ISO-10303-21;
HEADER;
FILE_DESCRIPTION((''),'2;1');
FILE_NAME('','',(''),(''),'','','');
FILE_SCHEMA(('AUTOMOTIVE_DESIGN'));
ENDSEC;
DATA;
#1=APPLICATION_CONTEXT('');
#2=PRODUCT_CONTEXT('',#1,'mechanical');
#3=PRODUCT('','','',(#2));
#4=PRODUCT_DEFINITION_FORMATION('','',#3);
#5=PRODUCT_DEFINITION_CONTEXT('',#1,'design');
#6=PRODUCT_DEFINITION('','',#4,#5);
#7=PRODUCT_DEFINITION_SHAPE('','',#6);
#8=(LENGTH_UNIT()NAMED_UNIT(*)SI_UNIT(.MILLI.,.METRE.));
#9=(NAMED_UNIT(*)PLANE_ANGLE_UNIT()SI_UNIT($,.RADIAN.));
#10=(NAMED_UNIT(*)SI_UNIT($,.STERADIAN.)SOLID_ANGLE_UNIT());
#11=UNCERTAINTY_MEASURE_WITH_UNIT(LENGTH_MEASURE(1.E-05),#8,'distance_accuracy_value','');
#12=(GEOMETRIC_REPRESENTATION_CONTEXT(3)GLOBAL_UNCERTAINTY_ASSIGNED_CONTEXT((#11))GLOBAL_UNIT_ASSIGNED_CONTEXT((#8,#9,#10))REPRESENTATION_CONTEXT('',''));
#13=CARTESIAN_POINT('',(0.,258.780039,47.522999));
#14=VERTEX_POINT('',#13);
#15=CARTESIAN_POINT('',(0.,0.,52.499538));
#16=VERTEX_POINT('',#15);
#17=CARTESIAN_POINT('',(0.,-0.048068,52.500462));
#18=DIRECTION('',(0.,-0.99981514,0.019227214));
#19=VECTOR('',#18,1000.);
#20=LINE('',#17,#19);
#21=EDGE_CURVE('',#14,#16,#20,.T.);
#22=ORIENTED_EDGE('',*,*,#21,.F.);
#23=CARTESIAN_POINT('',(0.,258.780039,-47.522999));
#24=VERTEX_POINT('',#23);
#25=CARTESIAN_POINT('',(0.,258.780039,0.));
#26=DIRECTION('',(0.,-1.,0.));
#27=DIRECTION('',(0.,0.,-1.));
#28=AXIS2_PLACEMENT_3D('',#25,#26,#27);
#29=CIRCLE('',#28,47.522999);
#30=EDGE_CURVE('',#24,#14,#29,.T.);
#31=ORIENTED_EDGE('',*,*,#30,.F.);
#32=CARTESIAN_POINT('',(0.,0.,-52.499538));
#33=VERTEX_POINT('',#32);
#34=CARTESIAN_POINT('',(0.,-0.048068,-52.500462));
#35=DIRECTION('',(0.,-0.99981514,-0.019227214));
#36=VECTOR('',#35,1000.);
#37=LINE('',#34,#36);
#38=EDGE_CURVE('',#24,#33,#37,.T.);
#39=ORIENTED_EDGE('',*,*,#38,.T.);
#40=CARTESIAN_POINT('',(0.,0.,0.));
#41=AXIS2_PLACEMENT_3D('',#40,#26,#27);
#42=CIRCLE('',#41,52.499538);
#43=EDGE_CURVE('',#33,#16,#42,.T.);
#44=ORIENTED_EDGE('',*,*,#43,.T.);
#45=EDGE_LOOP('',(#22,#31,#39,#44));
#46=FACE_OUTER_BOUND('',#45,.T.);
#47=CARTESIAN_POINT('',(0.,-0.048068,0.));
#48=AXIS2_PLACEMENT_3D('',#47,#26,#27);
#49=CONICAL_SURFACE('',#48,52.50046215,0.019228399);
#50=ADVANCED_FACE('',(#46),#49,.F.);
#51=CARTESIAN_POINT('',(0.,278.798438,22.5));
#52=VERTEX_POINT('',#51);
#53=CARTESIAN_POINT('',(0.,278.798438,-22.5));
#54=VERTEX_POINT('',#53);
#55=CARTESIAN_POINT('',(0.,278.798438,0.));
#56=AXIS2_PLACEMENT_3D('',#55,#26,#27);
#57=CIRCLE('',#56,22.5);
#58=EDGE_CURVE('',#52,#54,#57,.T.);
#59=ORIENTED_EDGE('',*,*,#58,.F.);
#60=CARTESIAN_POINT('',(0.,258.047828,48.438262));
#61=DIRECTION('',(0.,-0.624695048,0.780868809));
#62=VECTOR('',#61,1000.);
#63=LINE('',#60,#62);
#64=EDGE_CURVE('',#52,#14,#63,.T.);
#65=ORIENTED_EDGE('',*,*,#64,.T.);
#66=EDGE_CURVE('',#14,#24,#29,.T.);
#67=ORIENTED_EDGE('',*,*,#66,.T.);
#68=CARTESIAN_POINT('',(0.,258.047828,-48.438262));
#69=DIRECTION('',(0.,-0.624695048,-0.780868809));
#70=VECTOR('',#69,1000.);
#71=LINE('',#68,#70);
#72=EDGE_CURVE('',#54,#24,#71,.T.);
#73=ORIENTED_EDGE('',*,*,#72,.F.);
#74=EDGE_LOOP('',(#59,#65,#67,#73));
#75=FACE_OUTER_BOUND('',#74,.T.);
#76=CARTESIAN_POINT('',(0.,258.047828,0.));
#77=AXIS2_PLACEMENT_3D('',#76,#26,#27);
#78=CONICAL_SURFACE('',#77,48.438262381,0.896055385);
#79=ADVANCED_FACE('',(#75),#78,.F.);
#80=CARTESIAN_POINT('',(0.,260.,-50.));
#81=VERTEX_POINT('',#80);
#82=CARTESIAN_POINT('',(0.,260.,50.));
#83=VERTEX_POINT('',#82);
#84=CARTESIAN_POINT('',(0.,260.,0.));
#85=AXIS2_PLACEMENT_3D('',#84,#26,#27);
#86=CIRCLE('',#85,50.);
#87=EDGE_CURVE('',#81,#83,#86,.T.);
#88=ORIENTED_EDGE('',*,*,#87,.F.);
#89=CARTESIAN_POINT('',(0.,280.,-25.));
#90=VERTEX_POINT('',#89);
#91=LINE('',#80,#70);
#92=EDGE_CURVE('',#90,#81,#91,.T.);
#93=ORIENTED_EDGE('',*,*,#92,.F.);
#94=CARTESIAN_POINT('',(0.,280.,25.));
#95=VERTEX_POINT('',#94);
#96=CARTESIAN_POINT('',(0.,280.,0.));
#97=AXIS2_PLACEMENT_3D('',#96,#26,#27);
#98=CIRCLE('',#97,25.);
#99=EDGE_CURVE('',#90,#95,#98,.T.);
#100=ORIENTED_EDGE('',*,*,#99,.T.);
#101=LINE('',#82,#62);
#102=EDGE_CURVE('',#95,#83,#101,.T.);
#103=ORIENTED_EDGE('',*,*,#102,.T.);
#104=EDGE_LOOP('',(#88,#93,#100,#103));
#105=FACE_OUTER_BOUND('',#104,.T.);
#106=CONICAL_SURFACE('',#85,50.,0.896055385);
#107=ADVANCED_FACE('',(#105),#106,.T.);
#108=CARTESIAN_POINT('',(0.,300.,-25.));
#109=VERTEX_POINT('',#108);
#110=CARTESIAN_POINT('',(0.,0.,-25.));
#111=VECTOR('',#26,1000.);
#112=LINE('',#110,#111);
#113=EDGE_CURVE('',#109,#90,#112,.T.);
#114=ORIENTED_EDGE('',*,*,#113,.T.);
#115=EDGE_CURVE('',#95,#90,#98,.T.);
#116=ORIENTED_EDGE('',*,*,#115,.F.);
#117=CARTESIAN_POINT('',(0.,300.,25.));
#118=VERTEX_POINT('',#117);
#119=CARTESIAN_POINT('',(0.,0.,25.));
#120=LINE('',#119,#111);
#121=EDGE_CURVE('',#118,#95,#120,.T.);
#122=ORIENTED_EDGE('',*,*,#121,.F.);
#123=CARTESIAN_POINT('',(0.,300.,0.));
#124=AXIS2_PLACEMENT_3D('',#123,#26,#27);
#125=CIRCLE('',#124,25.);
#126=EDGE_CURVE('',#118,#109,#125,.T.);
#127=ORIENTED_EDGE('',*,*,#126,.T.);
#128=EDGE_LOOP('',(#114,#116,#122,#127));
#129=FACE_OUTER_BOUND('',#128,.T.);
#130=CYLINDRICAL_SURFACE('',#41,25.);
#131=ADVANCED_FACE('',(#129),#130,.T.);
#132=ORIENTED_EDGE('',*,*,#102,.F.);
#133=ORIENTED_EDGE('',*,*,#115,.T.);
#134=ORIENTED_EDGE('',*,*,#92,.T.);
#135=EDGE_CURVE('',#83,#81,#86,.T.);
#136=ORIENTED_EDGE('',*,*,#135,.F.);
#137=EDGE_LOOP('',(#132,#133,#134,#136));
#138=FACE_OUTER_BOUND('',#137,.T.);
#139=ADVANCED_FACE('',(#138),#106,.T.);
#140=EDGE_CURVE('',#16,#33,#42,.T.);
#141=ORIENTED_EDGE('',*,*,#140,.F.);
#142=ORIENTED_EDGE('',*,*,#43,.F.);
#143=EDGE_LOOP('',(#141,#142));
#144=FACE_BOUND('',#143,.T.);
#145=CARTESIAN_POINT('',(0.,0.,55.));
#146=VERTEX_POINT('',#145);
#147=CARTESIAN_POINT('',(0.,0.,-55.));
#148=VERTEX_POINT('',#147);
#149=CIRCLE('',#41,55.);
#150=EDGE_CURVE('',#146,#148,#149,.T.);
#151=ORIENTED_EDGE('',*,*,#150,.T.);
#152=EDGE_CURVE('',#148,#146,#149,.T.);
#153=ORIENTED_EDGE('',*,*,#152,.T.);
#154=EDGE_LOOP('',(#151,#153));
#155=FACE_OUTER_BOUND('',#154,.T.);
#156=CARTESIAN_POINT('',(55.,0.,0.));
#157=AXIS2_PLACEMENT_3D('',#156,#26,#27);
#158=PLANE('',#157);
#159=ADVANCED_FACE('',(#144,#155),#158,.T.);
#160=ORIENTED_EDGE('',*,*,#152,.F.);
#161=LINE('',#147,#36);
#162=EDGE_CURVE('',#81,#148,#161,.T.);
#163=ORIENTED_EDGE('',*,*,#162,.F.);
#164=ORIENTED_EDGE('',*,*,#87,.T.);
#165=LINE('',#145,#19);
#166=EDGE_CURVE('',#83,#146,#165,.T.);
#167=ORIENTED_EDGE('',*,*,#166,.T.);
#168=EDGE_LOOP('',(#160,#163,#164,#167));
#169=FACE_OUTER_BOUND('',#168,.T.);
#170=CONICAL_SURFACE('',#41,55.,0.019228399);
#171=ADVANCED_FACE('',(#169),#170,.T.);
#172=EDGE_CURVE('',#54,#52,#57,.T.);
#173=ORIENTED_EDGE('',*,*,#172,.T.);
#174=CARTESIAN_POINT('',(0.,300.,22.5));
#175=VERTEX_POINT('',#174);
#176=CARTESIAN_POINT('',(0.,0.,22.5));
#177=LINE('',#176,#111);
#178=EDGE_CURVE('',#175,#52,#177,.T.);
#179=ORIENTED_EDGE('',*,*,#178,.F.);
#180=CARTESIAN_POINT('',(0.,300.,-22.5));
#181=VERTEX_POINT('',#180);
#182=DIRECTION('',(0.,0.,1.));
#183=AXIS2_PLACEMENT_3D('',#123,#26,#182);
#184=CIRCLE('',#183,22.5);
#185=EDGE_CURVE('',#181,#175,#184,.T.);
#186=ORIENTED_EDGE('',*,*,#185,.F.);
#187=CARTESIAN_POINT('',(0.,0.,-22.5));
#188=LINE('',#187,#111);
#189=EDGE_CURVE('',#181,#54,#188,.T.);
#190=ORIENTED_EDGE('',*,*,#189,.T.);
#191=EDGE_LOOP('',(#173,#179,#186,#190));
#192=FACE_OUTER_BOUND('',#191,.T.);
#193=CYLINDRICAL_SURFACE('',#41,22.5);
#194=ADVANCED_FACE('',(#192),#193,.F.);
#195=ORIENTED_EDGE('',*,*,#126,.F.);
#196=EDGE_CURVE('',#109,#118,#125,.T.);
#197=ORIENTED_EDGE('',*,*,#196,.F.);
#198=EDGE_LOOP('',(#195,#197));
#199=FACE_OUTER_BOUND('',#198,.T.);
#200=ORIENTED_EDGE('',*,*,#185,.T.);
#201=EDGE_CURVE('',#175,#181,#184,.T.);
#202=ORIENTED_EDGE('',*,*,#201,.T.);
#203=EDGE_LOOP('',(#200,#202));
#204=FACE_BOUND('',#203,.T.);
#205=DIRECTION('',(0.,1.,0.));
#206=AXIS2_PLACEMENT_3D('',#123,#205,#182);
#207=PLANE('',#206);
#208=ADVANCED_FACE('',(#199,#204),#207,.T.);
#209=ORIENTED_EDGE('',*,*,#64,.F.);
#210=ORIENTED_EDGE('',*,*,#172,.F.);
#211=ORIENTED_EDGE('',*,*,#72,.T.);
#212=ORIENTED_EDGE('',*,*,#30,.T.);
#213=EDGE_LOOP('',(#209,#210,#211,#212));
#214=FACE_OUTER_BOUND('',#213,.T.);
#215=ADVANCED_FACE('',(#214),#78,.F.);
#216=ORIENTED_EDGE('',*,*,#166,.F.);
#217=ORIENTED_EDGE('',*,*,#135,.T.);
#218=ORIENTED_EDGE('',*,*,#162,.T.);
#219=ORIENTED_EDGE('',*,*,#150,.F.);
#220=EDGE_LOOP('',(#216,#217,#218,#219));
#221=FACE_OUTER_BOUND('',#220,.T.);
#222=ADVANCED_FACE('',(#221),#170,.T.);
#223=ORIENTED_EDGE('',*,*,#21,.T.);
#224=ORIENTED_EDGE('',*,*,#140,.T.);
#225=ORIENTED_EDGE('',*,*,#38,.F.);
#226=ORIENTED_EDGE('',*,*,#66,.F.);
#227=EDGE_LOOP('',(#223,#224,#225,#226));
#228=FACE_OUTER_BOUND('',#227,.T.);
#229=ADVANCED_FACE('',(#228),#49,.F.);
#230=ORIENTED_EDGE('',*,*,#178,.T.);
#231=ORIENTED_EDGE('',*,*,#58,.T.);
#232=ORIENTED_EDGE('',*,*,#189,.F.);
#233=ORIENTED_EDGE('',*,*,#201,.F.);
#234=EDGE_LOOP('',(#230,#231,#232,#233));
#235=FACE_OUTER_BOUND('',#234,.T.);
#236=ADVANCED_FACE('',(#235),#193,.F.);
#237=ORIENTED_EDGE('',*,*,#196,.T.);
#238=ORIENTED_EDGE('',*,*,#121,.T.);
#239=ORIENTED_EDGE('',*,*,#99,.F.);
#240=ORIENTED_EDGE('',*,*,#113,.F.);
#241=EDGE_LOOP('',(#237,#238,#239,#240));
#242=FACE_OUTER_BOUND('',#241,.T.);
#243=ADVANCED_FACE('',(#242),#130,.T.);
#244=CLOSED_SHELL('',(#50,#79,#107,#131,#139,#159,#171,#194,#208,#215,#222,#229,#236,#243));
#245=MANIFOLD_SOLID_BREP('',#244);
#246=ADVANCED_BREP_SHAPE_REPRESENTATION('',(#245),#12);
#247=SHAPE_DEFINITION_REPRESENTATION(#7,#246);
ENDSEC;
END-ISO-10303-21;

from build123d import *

# Parameters (mm, degrees)
SHELL1_T = -2.5


with BuildPart() as part:
    # Sketch1 → Revolve1 (revolve)
    with BuildSketch(Plane.XY, mode=Mode.PRIVATE) as revolve1_sk:
        Polygon((0, 0), (0, 300), (25, 300), (25, 280), (50, 260), (55, 0), align=None)
    revolve(revolve1_sk.sketch.rotate(Axis((0, 0, 0), (0, 1, 0)), 90), axis=Axis((0, 0, 0), (0, 1, 0)))

    # Shell1
    shell1_openings = [part.faces().sort_by_distance(p)[0] for p in [
        (0, 300, 0),
        (0, 0, 0),
    ]]
    offset(amount=SHELL1_T, openings=shell1_openings, kind=Kind.INTERSECTION)


solid = part.part
